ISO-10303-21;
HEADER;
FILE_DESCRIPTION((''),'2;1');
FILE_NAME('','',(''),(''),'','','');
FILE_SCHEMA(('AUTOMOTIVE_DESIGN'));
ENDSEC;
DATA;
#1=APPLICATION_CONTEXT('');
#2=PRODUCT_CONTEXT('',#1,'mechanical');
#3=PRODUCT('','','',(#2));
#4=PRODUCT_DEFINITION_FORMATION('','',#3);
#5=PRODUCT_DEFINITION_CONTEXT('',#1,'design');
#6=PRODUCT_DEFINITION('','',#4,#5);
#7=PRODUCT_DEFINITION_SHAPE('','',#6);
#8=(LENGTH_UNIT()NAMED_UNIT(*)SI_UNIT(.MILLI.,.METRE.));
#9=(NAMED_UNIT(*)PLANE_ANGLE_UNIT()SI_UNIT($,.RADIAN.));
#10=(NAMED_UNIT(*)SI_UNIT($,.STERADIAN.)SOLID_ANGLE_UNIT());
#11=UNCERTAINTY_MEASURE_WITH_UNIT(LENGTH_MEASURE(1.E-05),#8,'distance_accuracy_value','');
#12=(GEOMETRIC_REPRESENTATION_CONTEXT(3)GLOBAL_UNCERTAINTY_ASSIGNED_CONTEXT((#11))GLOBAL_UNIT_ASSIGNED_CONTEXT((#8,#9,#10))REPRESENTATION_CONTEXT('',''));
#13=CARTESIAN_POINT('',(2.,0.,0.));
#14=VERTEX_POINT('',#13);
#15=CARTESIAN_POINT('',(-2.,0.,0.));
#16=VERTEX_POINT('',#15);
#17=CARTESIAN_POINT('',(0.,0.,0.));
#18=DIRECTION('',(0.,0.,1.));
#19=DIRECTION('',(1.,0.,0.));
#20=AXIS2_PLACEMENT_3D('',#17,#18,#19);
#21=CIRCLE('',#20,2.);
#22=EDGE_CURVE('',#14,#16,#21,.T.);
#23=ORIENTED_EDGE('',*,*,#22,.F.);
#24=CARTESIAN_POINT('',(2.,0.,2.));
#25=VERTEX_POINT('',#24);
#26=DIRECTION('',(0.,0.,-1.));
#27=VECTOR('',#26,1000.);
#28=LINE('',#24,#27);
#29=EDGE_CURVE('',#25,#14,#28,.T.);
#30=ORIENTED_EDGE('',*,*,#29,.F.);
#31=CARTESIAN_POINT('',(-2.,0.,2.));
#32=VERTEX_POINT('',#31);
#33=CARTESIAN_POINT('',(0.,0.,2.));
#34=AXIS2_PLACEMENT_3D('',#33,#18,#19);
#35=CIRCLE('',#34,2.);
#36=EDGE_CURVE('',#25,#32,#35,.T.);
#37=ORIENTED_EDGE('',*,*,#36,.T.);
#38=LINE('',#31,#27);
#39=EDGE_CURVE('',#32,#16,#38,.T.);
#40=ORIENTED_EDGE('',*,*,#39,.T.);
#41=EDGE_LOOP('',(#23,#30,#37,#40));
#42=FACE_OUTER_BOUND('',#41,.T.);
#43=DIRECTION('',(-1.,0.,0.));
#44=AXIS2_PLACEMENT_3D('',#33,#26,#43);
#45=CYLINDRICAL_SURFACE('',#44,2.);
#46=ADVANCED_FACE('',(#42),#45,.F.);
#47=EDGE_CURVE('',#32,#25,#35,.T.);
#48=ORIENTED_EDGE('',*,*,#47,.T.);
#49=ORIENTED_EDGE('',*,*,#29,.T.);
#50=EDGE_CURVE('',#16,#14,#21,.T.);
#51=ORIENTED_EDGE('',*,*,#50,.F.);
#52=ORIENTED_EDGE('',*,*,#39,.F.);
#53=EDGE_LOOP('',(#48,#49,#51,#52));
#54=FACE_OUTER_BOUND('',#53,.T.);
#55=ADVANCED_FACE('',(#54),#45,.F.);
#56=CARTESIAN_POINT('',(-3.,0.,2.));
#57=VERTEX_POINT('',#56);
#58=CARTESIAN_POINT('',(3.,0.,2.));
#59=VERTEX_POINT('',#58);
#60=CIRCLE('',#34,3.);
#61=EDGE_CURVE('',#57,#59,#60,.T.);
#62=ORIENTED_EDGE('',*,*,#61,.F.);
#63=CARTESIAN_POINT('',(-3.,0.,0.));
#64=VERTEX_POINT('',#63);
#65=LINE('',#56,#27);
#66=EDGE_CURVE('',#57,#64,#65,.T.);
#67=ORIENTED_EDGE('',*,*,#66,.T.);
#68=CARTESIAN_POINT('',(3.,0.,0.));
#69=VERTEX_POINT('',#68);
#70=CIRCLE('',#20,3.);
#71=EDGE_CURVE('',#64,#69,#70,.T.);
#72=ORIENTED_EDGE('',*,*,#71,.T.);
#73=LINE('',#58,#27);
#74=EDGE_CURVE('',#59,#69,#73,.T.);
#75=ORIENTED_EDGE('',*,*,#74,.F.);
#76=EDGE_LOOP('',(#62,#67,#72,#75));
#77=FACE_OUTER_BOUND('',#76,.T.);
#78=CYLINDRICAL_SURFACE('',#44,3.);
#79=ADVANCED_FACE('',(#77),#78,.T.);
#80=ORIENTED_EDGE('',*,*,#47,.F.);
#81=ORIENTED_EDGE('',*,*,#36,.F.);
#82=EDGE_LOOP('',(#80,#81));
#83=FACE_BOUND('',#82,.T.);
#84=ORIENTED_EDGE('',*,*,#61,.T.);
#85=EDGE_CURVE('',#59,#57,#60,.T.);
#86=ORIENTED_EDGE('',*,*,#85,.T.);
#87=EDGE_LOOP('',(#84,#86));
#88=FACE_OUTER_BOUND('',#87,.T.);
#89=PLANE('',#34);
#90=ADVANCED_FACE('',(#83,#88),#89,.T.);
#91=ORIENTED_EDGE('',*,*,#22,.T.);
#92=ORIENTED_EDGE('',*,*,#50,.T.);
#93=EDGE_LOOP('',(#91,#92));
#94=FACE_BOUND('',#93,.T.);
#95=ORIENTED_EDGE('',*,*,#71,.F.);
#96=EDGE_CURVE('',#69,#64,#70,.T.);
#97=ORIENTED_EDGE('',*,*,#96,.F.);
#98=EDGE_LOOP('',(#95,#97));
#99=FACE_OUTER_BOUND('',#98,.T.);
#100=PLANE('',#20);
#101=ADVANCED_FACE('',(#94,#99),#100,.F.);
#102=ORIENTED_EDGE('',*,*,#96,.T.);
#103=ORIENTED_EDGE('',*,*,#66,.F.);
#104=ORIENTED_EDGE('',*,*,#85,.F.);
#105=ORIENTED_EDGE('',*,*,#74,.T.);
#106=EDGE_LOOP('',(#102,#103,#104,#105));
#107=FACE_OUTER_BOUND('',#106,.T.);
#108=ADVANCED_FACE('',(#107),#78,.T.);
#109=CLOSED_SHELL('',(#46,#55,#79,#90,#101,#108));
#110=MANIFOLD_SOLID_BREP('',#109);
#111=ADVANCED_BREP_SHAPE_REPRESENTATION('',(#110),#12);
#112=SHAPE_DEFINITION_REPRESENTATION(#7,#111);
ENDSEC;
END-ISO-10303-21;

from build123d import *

# Parameters (mm, degrees)
SKETCH1_R           = 3
SKETCH1_R_2         = 2
BOSS_EXTRUDE1_DEPTH = 2


with BuildPart() as part:
    # Sketch1 → Boss-Extrude1 (new body)
    with BuildSketch(Plane.XY):
        Circle(SKETCH1_R)
        Circle(SKETCH1_R_2, mode=Mode.SUBTRACT)
    extrude(amount=BOSS_EXTRUDE1_DEPTH)


solid = part.part
